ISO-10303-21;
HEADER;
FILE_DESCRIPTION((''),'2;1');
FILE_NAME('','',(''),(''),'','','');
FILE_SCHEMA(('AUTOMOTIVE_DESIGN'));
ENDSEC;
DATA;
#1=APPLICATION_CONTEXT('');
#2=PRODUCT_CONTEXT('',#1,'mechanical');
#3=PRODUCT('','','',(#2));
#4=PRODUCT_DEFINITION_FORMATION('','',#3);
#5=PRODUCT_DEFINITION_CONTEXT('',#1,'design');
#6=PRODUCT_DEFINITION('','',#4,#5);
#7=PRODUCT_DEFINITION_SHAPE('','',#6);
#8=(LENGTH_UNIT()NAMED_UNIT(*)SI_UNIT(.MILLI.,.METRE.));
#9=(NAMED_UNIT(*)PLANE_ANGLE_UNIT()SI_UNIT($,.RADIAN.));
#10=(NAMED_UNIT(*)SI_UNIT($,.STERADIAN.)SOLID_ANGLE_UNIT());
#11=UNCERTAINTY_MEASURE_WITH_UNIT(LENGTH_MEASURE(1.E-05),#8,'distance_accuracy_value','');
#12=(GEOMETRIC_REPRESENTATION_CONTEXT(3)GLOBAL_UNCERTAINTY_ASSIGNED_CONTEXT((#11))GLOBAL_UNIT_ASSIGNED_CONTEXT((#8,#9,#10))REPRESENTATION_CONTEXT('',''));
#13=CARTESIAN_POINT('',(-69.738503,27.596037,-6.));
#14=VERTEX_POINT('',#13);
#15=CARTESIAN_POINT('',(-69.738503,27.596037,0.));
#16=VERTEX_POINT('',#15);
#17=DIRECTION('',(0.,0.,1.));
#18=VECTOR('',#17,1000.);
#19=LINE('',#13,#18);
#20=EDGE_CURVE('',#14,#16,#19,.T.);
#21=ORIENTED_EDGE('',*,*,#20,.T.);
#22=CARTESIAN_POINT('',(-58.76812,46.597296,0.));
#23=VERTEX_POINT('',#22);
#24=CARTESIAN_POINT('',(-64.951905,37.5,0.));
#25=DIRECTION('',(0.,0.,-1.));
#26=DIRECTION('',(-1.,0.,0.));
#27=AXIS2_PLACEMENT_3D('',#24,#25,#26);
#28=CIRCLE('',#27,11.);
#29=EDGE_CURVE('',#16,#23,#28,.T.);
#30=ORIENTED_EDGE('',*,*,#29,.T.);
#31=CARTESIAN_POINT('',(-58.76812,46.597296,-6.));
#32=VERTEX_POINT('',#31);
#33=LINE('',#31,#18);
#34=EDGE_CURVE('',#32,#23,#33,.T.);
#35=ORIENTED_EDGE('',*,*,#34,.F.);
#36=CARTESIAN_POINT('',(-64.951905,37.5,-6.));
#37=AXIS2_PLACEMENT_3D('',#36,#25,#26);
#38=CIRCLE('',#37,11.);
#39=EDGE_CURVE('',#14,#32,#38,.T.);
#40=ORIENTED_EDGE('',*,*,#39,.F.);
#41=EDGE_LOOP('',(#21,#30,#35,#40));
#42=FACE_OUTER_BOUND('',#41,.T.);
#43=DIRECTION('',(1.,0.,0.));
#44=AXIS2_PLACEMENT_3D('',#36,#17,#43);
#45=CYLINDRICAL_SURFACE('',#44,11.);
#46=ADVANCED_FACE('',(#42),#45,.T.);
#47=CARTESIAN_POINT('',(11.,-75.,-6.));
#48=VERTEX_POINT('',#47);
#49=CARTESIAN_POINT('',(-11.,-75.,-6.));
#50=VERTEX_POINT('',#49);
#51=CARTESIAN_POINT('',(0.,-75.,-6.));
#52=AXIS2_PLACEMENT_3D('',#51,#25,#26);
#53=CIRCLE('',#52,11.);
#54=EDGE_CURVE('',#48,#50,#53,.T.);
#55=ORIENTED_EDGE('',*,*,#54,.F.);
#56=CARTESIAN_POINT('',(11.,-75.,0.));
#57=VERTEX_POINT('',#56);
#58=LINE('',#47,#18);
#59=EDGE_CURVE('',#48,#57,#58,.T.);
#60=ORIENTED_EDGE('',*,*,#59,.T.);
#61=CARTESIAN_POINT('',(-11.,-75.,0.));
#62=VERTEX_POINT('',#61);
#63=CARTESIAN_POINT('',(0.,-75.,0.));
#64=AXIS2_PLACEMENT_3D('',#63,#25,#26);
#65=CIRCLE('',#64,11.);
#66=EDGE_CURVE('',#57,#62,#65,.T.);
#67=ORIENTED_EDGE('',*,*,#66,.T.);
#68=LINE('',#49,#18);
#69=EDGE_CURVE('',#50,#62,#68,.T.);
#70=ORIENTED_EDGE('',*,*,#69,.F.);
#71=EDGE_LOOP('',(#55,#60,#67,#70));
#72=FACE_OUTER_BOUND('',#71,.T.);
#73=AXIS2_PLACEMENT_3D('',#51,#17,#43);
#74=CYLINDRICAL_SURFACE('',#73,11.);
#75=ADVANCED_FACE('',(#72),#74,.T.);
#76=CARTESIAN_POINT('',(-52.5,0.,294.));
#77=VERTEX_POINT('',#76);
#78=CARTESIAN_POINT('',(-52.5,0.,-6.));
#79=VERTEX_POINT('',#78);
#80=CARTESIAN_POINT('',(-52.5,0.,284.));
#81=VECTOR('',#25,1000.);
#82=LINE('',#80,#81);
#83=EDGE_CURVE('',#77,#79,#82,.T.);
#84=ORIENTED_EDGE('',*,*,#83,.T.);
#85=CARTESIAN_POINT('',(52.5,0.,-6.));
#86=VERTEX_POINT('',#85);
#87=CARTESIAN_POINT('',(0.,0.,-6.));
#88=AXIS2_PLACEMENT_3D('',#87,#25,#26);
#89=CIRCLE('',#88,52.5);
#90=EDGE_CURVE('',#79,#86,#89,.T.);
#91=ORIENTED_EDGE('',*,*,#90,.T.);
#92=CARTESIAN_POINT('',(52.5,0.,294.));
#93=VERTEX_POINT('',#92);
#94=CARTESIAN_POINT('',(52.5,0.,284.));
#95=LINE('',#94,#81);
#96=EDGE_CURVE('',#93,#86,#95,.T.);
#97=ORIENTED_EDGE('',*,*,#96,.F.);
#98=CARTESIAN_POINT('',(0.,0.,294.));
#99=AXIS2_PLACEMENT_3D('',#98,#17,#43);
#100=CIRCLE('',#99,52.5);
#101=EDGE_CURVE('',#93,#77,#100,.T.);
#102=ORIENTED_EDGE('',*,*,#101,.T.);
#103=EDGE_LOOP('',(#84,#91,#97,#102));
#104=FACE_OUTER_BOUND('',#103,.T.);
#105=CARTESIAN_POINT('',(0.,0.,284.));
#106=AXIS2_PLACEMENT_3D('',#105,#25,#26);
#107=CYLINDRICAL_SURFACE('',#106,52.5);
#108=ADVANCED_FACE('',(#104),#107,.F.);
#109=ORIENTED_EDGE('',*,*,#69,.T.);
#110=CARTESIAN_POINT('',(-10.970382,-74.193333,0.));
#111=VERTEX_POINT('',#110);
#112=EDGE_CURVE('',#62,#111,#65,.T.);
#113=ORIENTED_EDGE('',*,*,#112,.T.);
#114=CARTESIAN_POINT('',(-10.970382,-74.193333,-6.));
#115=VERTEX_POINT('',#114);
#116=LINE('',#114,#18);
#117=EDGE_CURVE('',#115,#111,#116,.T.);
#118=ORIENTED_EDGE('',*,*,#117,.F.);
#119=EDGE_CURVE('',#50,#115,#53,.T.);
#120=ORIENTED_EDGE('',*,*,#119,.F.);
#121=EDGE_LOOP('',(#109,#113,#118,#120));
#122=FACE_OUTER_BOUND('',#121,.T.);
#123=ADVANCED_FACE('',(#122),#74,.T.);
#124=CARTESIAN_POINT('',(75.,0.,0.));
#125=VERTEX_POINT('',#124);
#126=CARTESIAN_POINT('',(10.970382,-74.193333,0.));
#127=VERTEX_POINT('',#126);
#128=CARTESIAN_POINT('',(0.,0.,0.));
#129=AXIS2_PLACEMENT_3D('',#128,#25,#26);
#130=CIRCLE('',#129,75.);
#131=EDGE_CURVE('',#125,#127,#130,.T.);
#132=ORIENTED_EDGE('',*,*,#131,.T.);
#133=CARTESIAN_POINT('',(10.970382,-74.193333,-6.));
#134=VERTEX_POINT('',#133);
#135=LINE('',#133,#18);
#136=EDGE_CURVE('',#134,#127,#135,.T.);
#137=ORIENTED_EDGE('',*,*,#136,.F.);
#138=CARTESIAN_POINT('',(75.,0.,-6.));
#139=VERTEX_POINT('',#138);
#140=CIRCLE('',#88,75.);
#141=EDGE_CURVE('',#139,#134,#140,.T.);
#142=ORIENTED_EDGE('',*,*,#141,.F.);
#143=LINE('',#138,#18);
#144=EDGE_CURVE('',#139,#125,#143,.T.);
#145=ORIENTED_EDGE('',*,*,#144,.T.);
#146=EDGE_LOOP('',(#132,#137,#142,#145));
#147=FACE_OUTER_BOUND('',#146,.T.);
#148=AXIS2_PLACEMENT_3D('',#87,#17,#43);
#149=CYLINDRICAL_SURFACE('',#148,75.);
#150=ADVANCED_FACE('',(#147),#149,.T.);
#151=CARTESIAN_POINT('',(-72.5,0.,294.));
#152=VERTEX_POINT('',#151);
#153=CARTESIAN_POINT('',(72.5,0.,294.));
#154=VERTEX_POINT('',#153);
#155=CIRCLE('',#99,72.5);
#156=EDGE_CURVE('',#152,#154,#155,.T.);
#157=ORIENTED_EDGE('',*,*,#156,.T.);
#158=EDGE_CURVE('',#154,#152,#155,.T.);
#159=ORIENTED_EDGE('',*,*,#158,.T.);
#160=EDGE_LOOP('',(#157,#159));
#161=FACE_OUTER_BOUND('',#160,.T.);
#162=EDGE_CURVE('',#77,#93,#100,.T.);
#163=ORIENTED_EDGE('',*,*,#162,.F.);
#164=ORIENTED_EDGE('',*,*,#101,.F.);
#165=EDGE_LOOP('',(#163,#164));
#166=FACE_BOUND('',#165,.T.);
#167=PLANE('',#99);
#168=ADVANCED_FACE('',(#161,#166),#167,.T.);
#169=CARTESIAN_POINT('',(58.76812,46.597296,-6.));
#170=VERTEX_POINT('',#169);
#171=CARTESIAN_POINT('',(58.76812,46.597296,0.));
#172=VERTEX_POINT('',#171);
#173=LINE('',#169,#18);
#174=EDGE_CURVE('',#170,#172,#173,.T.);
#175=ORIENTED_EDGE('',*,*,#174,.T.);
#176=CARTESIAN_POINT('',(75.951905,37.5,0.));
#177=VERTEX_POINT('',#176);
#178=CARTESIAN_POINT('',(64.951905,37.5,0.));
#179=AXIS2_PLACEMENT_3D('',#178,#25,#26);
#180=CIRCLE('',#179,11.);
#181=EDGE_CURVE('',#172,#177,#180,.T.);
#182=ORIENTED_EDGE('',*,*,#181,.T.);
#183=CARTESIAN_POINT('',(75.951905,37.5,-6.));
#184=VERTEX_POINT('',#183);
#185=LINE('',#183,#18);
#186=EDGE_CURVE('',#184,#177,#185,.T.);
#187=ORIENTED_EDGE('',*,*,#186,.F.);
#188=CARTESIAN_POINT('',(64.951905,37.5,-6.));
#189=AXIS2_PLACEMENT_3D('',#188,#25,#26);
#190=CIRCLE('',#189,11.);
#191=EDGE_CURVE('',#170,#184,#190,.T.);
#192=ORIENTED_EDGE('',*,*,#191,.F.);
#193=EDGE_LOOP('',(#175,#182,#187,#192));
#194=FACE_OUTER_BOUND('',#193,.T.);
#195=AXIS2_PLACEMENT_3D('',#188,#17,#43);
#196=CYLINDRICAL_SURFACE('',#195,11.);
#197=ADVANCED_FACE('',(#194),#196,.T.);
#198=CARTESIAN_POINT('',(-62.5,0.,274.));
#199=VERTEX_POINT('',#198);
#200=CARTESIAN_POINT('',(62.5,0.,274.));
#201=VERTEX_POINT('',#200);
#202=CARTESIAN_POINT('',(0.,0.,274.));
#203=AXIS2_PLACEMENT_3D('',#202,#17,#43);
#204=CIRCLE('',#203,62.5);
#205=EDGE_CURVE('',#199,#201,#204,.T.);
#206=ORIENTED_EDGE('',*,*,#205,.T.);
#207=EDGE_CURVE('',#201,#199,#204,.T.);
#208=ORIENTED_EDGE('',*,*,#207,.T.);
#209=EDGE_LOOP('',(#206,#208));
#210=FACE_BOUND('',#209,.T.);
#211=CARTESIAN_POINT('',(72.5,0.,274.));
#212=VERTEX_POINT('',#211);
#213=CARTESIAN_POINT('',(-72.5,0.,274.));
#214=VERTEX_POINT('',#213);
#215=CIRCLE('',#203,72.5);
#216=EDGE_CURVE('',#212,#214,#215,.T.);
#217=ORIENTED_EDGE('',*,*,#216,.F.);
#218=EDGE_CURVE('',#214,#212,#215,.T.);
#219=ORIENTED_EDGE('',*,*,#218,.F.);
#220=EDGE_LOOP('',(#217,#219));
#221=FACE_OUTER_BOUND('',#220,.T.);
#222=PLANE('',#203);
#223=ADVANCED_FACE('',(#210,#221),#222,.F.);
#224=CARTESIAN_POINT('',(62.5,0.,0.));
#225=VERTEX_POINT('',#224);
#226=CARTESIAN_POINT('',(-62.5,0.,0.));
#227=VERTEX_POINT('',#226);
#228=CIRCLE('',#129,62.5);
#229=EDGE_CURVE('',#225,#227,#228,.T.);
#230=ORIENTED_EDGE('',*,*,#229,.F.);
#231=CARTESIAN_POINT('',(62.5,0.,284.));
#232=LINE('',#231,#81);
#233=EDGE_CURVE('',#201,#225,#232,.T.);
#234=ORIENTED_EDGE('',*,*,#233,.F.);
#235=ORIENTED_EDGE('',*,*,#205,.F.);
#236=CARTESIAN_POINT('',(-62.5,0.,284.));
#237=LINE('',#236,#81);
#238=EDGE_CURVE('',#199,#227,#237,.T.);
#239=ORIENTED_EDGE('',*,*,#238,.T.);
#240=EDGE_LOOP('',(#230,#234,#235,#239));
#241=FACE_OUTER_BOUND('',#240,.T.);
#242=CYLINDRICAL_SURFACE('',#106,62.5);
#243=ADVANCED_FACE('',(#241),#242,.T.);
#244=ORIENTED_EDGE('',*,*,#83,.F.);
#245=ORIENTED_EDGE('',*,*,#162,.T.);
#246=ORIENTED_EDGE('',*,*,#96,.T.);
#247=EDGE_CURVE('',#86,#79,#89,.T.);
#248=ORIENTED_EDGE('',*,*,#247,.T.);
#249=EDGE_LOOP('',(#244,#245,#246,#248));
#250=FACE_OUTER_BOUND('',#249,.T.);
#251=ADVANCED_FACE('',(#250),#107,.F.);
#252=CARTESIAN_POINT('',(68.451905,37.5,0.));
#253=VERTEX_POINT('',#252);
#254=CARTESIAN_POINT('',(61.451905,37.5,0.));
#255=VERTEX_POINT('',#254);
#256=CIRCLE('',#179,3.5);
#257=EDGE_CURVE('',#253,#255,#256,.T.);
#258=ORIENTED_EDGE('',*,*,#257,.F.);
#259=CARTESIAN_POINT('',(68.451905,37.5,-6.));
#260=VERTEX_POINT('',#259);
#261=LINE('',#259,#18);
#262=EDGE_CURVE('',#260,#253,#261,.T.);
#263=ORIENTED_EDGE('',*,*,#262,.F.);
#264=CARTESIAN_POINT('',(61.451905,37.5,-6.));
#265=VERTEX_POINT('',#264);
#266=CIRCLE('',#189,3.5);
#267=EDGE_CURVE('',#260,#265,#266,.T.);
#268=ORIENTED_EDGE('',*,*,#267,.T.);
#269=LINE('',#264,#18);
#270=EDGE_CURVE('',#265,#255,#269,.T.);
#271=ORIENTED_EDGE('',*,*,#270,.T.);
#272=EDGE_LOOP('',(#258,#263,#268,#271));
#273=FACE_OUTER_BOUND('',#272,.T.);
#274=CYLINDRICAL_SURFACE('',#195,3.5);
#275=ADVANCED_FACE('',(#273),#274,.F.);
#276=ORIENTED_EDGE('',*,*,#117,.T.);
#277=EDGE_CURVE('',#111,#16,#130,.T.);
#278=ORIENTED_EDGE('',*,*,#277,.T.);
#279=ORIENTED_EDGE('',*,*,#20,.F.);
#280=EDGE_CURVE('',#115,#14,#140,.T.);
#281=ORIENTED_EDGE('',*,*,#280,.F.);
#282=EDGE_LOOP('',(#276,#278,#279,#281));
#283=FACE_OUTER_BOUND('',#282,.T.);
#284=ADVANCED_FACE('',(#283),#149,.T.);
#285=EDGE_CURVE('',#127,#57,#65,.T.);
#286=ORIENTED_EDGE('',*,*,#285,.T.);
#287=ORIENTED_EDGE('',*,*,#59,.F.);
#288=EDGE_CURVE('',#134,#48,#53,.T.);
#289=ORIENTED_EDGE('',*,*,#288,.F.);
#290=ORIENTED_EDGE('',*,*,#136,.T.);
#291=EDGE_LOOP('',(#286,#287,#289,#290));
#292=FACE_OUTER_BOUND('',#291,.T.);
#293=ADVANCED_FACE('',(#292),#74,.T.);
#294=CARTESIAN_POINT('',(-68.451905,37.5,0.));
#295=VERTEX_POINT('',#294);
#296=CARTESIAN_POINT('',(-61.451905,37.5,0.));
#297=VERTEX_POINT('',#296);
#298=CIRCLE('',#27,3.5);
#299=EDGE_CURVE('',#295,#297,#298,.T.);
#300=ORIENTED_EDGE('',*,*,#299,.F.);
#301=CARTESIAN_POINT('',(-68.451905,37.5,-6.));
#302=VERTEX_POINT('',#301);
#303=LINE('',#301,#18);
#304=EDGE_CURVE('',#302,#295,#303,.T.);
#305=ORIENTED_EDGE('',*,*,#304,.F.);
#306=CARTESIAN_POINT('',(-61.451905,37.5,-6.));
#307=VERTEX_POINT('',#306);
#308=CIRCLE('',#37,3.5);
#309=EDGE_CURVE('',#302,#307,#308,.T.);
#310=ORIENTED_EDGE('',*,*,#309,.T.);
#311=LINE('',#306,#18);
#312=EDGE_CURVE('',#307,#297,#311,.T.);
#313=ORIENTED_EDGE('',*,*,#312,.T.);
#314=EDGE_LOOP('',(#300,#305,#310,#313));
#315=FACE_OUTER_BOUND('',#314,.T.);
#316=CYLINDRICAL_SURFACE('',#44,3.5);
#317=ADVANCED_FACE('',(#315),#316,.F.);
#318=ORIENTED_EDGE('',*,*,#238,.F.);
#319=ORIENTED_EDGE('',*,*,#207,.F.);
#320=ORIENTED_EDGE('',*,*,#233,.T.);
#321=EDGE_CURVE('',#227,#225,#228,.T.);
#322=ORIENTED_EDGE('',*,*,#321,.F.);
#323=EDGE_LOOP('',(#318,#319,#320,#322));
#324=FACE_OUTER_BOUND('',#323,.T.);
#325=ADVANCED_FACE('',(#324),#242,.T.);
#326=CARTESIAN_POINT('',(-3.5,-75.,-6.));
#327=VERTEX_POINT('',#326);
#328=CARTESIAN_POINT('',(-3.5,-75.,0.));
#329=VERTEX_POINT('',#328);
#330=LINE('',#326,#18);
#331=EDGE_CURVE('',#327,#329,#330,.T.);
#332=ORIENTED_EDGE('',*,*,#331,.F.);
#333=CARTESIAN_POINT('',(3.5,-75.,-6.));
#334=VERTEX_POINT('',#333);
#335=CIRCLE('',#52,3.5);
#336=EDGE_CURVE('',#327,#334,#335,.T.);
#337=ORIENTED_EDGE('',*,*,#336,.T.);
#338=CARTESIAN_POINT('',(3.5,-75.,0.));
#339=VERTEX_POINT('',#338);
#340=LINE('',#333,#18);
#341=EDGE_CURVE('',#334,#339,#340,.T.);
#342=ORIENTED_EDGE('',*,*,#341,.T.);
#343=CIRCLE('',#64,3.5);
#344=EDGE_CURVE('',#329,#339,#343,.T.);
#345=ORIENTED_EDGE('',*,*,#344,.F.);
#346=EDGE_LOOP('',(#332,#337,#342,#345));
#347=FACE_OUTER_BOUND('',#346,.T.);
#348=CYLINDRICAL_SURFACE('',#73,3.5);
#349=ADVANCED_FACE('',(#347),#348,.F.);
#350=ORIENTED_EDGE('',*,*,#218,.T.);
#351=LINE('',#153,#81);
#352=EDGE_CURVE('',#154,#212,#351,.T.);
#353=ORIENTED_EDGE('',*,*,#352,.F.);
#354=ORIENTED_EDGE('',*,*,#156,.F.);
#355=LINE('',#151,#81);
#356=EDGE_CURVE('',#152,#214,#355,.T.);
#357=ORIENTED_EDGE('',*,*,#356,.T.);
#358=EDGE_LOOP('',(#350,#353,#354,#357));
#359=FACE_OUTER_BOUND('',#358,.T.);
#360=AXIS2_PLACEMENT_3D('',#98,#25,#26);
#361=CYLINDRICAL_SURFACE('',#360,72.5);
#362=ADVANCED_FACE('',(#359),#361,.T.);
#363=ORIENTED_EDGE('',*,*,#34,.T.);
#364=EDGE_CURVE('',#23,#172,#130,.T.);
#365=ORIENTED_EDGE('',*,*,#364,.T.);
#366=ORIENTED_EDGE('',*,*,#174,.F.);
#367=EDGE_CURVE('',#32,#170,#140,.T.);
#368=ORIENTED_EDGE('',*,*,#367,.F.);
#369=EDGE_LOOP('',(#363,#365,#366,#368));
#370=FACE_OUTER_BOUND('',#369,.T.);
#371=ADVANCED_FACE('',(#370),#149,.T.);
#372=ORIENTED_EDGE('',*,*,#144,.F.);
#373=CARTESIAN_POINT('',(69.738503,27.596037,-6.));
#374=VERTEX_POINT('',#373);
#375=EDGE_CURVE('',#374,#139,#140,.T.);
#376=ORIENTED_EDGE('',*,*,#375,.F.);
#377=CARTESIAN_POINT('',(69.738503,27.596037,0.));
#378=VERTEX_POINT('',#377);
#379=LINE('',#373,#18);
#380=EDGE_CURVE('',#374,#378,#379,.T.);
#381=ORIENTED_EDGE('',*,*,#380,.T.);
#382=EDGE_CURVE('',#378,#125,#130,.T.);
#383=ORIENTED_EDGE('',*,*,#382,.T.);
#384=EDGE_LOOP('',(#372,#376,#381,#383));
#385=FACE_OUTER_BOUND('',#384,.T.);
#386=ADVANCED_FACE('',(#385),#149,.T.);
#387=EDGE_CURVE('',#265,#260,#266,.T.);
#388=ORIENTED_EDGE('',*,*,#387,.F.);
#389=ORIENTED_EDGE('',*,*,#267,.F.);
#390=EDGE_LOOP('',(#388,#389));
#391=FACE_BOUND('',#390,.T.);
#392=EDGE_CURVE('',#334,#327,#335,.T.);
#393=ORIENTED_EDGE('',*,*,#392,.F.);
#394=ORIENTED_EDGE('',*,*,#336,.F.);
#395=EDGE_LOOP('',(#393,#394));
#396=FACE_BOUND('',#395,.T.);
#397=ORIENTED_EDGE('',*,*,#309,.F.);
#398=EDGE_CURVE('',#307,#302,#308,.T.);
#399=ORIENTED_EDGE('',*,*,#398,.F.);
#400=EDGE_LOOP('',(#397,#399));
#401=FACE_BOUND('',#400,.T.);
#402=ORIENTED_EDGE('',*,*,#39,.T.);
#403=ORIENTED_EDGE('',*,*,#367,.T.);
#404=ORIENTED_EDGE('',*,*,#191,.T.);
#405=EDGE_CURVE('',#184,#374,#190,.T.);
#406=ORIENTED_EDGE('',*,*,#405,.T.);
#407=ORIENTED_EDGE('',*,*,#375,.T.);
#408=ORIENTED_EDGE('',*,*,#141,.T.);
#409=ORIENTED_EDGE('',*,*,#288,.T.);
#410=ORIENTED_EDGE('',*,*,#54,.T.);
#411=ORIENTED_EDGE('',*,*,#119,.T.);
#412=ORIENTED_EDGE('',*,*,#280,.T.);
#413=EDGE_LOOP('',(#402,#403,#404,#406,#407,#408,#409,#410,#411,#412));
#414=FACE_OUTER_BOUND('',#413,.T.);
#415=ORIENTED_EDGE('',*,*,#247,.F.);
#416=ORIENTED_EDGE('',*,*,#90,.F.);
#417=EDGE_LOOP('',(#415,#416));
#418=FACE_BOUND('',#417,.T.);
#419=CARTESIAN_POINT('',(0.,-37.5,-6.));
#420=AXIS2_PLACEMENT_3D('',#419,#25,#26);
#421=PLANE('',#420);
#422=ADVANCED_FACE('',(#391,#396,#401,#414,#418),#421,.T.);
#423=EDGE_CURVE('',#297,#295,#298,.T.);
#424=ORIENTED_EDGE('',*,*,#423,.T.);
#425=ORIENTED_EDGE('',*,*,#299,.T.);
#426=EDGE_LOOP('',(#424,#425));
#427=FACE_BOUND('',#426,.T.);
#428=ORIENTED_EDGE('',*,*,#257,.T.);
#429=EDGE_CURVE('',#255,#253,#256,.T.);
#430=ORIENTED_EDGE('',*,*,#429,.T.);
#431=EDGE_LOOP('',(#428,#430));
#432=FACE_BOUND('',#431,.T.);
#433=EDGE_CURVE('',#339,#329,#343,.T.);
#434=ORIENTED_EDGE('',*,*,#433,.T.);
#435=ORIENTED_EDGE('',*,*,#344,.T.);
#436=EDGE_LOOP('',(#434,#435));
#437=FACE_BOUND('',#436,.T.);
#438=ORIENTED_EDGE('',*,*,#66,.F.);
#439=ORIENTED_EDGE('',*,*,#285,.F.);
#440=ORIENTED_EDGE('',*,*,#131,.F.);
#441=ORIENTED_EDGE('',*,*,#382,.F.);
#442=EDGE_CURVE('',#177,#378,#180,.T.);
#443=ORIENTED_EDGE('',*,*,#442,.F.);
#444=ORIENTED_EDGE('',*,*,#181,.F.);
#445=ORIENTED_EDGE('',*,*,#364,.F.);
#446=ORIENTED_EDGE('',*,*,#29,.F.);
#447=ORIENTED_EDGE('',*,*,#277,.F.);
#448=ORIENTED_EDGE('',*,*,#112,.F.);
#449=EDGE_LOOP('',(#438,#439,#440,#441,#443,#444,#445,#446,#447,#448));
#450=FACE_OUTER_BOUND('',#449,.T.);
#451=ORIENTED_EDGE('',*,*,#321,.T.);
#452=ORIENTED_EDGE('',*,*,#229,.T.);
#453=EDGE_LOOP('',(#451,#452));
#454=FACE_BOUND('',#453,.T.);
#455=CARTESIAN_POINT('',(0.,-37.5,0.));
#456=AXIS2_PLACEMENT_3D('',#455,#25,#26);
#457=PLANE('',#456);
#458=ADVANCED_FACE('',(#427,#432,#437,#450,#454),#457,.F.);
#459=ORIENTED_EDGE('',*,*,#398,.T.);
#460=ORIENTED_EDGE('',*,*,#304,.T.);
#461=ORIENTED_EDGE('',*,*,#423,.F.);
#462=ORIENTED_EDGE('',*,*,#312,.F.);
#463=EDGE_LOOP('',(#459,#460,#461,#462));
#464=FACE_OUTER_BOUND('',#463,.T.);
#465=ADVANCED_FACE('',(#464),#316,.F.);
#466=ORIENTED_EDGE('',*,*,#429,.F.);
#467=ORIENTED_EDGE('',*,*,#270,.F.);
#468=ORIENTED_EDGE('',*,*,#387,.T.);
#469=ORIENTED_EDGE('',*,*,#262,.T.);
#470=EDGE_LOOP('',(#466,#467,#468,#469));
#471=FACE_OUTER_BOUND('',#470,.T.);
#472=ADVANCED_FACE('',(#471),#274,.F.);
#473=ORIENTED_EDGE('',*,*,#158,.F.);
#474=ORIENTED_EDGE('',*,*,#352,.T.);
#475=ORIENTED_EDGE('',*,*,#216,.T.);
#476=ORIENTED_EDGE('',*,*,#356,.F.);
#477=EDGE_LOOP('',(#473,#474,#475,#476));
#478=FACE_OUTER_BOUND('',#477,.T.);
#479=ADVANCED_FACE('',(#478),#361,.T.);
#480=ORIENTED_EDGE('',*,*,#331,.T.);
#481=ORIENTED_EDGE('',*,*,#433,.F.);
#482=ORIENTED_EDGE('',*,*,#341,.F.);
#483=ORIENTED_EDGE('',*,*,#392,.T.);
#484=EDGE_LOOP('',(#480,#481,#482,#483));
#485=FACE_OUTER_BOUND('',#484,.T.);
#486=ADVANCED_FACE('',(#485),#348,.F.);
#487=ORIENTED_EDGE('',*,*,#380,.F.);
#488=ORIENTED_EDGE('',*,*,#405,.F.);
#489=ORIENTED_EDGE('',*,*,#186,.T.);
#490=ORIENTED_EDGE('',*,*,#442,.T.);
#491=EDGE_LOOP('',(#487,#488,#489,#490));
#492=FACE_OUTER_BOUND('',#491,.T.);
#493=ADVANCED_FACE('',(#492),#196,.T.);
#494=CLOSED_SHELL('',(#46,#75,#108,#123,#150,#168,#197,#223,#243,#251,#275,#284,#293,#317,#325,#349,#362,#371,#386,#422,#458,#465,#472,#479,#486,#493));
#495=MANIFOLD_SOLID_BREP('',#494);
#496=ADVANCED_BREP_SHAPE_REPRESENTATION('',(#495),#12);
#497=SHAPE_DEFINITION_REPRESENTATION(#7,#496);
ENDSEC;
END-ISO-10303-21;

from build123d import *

# Parameters (mm, degrees)
SKETCH_1_R      = 62.5
SKETCH_1_R_2    = 52.5
EXTRUDE_1_DEPTH = 284
SKETCH_2_R      = 72.5
SKETCH_2_R_2    = 52.5
EXTRUDE_2_DEPTH = 10
EXTRUDE_START   = 6
SKETCH_3_R      = 52.5
SKETCH_3_R_2    = 3.5
EXTRUDE_3_DEPTH = 6


with BuildPart() as part:
    # 草图1 → 凸台-拉伸1 (new body)
    with BuildSketch(Plane.XY):
        Circle(SKETCH_1_R)
        Circle(SKETCH_1_R_2, mode=Mode.SUBTRACT)
    extrude(amount=EXTRUDE_1_DEPTH)

    # 草图2 → 凸台-拉伸2 (add, symmetric)
    with BuildSketch(Plane.XY.offset(284)):
        Circle(SKETCH_2_R)
        Circle(SKETCH_2_R_2, mode=Mode.SUBTRACT)
    extrude(amount=EXTRUDE_2_DEPTH, both=True)

    # 草图3 → 凸台-拉伸3 (add)
    with BuildSketch(Plane(origin=(0, 0, 0), x_dir=(-1, 0, 0), z_dir=(0, 0, -1)).offset(EXTRUDE_START)):
        with BuildLine():
            ThreePointArc((10.970382349, -74.193333333), (64.951905284, -37.5), (69.738502633, 27.596036863))
            ThreePointArc((69.738502633, 27.596036863), (74.478184725, 43), (58.768120283, 46.59729647))
            ThreePointArc((58.768120283, 46.59729647), (0, 75), (-58.768120283, 46.59729647))
            ThreePointArc((-58.768120283, 46.59729647), (-74.478184725, 43), (-69.738502633, 27.596036863))
            ThreePointArc((-69.738502633, 27.596036863), (-64.951905284, -37.5), (-10.970382349, -74.193333333))
            ThreePointArc((-10.970382349, -74.193333333), (0, -86), (10.970382349, -74.193333333))
        make_face()
        Circle(SKETCH_3_R, mode=Mode.SUBTRACT)
        with Locations((0, -75)):
            Circle(SKETCH_3_R_2, mode=Mode.SUBTRACT)
        with Locations((-64.951905284, 37.5)):
            Circle(SKETCH_3_R_2, mode=Mode.SUBTRACT)
        with Locations((64.951905284, 37.5)):
            Circle(SKETCH_3_R_2, mode=Mode.SUBTRACT)
    extrude(amount=-EXTRUDE_3_DEPTH)


solid = part.part
